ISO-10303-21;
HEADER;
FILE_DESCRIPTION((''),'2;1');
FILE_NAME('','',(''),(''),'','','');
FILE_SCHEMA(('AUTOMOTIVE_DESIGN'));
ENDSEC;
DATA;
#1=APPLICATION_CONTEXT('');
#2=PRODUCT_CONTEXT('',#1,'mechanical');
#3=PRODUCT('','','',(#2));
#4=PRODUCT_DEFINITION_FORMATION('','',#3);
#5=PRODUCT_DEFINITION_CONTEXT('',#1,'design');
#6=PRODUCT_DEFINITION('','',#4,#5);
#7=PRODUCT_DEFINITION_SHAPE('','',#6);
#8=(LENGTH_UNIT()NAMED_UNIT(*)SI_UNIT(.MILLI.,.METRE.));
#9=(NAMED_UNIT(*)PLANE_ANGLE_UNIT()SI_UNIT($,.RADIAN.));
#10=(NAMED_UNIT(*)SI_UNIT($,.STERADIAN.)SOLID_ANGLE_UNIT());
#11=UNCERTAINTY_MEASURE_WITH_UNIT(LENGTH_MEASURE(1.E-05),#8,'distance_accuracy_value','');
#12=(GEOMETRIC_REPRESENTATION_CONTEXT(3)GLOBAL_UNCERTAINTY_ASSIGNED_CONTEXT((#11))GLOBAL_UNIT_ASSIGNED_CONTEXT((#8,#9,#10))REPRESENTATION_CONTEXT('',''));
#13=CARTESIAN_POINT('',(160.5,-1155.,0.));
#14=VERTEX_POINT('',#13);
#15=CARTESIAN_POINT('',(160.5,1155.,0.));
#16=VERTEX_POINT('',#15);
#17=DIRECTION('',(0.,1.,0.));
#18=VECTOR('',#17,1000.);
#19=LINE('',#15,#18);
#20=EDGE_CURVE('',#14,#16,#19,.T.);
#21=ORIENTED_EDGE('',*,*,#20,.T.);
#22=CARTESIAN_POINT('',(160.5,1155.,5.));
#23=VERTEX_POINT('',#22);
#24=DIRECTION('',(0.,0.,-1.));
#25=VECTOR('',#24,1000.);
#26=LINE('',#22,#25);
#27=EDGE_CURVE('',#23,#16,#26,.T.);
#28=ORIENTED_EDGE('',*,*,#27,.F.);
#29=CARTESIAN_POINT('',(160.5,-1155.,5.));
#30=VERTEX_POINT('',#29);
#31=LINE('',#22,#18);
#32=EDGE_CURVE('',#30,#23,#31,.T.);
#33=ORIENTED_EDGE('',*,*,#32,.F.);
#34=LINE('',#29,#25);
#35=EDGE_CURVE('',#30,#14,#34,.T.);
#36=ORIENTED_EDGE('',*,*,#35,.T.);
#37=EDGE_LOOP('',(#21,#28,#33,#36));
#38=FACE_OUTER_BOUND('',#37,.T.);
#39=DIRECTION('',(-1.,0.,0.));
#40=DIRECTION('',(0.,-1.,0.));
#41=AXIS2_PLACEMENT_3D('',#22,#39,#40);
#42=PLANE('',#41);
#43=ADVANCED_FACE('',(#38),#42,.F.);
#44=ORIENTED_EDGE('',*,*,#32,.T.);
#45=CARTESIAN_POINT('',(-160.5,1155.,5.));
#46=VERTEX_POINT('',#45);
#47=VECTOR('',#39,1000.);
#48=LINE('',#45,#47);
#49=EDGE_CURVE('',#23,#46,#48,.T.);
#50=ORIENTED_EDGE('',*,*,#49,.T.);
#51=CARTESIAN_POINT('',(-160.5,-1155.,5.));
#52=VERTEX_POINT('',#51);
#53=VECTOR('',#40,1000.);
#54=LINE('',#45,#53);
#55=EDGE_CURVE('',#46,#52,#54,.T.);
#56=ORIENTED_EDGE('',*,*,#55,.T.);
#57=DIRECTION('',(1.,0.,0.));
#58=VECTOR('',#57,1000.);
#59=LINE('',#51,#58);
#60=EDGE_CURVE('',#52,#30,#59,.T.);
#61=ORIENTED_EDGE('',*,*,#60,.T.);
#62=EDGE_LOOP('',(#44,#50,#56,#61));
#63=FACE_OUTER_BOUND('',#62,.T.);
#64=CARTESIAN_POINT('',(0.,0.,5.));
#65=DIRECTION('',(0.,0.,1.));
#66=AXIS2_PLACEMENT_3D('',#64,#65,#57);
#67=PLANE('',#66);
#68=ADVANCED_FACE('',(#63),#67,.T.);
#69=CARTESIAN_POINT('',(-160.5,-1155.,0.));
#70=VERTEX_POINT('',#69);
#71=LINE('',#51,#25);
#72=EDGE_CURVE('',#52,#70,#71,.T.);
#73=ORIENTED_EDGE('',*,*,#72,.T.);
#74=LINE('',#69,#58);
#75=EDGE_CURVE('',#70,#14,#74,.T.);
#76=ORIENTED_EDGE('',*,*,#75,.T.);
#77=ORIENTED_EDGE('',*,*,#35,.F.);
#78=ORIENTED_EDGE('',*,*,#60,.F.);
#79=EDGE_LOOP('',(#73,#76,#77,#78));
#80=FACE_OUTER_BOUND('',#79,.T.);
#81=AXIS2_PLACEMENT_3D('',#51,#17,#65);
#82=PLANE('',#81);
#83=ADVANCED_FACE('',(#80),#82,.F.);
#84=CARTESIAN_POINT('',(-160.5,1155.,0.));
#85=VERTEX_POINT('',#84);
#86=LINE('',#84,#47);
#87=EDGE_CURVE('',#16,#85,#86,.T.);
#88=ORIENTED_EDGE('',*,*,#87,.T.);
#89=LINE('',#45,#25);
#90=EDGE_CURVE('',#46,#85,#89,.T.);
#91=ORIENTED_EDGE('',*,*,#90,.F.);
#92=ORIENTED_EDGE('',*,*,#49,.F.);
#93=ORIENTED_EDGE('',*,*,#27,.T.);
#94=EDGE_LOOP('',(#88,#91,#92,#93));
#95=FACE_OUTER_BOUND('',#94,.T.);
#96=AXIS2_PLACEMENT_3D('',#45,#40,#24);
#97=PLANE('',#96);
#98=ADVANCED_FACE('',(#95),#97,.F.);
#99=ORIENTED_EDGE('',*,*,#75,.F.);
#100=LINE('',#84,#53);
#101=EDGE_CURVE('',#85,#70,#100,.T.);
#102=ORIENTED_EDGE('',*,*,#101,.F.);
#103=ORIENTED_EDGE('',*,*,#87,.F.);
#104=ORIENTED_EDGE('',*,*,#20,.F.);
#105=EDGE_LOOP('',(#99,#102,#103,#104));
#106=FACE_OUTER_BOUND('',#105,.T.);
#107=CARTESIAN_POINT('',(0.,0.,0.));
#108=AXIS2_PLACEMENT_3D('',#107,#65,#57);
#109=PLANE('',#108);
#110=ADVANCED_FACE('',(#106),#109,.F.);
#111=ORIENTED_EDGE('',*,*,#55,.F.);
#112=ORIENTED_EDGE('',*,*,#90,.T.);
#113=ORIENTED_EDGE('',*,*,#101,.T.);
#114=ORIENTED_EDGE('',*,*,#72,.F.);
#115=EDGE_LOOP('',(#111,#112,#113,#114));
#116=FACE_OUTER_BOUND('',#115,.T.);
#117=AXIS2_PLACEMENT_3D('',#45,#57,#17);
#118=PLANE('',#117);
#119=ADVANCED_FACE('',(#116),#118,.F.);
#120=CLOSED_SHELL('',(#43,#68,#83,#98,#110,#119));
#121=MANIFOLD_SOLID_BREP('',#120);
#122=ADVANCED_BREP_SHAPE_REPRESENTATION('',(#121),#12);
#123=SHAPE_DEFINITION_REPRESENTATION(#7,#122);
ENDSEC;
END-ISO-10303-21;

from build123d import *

# Parameters (mm, degrees)
SKETCH_1_W      = 321
SKETCH_1_H      = 2310
EXTRUDE_1_DEPTH = 5


with BuildPart() as part:
    # 草图1 → 凸台-拉伸1 (new body)
    with BuildSketch(Plane.XY):
        Rectangle(SKETCH_1_W, SKETCH_1_H)
    extrude(amount=EXTRUDE_1_DEPTH)


solid = part.part
